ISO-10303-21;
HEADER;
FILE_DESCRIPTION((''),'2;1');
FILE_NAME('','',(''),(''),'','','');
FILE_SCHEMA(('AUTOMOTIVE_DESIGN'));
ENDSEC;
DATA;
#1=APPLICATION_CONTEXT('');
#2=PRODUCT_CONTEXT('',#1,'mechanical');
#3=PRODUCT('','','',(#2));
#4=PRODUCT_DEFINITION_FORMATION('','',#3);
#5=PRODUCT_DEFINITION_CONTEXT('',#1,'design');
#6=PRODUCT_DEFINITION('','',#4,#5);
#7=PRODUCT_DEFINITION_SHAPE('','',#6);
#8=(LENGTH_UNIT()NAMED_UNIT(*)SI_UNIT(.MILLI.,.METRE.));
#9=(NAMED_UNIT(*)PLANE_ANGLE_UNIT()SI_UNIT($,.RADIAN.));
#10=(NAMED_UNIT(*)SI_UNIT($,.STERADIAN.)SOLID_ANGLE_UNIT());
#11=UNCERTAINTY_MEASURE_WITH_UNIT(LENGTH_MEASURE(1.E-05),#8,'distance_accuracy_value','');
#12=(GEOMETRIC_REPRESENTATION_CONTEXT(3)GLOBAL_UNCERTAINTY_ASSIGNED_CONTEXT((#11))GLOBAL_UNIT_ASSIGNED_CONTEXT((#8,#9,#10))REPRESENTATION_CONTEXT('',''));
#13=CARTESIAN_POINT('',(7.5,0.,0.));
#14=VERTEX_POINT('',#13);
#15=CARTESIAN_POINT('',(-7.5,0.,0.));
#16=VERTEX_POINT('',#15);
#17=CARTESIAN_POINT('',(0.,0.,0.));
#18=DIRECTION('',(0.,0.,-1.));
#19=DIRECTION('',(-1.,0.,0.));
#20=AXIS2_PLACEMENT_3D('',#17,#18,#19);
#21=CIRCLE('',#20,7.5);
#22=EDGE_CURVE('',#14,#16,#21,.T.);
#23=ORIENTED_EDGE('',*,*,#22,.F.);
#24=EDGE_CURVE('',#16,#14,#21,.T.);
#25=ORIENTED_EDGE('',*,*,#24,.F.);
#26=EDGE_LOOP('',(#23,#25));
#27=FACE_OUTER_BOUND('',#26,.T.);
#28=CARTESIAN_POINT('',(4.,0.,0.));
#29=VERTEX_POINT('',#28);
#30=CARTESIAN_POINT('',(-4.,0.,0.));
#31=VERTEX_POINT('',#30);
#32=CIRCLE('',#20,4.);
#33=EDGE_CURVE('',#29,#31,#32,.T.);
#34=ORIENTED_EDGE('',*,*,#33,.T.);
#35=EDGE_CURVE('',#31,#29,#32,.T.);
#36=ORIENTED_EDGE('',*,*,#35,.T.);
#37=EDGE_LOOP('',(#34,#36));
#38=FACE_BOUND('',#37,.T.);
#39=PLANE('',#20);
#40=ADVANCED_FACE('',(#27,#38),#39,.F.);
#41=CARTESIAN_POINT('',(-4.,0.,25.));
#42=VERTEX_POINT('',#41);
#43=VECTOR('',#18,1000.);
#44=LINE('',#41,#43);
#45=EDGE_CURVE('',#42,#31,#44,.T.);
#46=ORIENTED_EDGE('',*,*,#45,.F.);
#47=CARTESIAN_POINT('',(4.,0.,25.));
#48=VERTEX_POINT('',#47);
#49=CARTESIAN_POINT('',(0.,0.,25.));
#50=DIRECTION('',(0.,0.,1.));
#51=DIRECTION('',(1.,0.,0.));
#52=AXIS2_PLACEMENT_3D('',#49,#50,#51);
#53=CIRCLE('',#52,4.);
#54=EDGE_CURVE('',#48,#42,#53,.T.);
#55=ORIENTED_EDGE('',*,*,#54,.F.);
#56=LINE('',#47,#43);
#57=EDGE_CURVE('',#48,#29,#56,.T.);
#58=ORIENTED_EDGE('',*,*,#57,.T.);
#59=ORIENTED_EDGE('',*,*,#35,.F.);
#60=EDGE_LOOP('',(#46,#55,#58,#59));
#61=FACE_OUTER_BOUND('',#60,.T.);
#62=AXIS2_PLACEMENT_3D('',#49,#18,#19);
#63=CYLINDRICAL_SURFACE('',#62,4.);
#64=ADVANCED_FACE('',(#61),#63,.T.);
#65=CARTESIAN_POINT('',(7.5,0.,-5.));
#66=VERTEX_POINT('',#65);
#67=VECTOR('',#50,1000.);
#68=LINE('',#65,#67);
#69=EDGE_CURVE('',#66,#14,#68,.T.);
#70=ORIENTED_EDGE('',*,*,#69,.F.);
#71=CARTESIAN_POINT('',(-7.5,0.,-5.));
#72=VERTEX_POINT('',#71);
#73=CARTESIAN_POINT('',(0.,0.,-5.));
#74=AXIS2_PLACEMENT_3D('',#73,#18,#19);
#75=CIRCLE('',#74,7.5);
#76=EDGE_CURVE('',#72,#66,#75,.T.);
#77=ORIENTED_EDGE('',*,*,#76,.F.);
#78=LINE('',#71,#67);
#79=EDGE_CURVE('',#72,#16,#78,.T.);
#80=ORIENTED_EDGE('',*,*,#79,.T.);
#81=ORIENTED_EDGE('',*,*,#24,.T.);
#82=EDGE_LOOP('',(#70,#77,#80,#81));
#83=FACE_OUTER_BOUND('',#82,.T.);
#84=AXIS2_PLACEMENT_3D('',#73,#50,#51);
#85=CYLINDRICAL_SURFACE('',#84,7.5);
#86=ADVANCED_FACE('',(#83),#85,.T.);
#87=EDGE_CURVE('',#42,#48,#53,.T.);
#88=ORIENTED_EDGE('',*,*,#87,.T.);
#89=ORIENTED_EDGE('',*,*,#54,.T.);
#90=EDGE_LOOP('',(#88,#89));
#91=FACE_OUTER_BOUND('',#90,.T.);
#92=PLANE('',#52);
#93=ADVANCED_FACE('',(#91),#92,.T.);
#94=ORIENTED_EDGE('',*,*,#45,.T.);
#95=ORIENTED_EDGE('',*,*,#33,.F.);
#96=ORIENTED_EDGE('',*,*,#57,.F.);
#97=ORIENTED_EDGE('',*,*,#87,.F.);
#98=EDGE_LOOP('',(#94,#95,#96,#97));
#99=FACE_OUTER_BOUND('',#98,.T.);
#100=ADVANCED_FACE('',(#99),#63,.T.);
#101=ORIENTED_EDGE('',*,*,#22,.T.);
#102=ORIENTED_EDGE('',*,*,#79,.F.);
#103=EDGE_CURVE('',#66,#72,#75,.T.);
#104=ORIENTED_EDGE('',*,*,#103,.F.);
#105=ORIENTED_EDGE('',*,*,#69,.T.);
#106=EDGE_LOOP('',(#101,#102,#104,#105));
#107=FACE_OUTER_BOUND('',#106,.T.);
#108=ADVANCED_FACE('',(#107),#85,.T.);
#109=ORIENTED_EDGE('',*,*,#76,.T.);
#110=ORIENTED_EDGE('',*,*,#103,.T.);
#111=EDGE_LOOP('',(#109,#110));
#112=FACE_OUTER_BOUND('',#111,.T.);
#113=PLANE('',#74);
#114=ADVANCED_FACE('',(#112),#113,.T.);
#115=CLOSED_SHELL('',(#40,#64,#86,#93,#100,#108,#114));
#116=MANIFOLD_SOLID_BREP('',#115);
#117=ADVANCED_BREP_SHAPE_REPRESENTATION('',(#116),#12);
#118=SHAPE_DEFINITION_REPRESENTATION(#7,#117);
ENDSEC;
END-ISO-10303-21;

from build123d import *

# Parameters (mm, degrees)
SKETCH1_R           = 4
BOSS_EXTRUDE1_DEPTH = 25
SKETCH2_R           = 7.5
BOSS_EXTRUDE2_DEPTH = 5


with BuildPart() as part:
    # Sketch1 → Boss-Extrude1 (new body)
    with BuildSketch(Plane.XY):
        Circle(SKETCH1_R)
    extrude(amount=BOSS_EXTRUDE1_DEPTH)

    # Sketch2 → Boss-Extrude2 (add)
    with BuildSketch(Plane(origin=(0, 0, 0), x_dir=(-1, 0, 0), z_dir=(0, 0, -1))):
        Circle(SKETCH2_R)
    extrude(amount=BOSS_EXTRUDE2_DEPTH)


solid = part.part
